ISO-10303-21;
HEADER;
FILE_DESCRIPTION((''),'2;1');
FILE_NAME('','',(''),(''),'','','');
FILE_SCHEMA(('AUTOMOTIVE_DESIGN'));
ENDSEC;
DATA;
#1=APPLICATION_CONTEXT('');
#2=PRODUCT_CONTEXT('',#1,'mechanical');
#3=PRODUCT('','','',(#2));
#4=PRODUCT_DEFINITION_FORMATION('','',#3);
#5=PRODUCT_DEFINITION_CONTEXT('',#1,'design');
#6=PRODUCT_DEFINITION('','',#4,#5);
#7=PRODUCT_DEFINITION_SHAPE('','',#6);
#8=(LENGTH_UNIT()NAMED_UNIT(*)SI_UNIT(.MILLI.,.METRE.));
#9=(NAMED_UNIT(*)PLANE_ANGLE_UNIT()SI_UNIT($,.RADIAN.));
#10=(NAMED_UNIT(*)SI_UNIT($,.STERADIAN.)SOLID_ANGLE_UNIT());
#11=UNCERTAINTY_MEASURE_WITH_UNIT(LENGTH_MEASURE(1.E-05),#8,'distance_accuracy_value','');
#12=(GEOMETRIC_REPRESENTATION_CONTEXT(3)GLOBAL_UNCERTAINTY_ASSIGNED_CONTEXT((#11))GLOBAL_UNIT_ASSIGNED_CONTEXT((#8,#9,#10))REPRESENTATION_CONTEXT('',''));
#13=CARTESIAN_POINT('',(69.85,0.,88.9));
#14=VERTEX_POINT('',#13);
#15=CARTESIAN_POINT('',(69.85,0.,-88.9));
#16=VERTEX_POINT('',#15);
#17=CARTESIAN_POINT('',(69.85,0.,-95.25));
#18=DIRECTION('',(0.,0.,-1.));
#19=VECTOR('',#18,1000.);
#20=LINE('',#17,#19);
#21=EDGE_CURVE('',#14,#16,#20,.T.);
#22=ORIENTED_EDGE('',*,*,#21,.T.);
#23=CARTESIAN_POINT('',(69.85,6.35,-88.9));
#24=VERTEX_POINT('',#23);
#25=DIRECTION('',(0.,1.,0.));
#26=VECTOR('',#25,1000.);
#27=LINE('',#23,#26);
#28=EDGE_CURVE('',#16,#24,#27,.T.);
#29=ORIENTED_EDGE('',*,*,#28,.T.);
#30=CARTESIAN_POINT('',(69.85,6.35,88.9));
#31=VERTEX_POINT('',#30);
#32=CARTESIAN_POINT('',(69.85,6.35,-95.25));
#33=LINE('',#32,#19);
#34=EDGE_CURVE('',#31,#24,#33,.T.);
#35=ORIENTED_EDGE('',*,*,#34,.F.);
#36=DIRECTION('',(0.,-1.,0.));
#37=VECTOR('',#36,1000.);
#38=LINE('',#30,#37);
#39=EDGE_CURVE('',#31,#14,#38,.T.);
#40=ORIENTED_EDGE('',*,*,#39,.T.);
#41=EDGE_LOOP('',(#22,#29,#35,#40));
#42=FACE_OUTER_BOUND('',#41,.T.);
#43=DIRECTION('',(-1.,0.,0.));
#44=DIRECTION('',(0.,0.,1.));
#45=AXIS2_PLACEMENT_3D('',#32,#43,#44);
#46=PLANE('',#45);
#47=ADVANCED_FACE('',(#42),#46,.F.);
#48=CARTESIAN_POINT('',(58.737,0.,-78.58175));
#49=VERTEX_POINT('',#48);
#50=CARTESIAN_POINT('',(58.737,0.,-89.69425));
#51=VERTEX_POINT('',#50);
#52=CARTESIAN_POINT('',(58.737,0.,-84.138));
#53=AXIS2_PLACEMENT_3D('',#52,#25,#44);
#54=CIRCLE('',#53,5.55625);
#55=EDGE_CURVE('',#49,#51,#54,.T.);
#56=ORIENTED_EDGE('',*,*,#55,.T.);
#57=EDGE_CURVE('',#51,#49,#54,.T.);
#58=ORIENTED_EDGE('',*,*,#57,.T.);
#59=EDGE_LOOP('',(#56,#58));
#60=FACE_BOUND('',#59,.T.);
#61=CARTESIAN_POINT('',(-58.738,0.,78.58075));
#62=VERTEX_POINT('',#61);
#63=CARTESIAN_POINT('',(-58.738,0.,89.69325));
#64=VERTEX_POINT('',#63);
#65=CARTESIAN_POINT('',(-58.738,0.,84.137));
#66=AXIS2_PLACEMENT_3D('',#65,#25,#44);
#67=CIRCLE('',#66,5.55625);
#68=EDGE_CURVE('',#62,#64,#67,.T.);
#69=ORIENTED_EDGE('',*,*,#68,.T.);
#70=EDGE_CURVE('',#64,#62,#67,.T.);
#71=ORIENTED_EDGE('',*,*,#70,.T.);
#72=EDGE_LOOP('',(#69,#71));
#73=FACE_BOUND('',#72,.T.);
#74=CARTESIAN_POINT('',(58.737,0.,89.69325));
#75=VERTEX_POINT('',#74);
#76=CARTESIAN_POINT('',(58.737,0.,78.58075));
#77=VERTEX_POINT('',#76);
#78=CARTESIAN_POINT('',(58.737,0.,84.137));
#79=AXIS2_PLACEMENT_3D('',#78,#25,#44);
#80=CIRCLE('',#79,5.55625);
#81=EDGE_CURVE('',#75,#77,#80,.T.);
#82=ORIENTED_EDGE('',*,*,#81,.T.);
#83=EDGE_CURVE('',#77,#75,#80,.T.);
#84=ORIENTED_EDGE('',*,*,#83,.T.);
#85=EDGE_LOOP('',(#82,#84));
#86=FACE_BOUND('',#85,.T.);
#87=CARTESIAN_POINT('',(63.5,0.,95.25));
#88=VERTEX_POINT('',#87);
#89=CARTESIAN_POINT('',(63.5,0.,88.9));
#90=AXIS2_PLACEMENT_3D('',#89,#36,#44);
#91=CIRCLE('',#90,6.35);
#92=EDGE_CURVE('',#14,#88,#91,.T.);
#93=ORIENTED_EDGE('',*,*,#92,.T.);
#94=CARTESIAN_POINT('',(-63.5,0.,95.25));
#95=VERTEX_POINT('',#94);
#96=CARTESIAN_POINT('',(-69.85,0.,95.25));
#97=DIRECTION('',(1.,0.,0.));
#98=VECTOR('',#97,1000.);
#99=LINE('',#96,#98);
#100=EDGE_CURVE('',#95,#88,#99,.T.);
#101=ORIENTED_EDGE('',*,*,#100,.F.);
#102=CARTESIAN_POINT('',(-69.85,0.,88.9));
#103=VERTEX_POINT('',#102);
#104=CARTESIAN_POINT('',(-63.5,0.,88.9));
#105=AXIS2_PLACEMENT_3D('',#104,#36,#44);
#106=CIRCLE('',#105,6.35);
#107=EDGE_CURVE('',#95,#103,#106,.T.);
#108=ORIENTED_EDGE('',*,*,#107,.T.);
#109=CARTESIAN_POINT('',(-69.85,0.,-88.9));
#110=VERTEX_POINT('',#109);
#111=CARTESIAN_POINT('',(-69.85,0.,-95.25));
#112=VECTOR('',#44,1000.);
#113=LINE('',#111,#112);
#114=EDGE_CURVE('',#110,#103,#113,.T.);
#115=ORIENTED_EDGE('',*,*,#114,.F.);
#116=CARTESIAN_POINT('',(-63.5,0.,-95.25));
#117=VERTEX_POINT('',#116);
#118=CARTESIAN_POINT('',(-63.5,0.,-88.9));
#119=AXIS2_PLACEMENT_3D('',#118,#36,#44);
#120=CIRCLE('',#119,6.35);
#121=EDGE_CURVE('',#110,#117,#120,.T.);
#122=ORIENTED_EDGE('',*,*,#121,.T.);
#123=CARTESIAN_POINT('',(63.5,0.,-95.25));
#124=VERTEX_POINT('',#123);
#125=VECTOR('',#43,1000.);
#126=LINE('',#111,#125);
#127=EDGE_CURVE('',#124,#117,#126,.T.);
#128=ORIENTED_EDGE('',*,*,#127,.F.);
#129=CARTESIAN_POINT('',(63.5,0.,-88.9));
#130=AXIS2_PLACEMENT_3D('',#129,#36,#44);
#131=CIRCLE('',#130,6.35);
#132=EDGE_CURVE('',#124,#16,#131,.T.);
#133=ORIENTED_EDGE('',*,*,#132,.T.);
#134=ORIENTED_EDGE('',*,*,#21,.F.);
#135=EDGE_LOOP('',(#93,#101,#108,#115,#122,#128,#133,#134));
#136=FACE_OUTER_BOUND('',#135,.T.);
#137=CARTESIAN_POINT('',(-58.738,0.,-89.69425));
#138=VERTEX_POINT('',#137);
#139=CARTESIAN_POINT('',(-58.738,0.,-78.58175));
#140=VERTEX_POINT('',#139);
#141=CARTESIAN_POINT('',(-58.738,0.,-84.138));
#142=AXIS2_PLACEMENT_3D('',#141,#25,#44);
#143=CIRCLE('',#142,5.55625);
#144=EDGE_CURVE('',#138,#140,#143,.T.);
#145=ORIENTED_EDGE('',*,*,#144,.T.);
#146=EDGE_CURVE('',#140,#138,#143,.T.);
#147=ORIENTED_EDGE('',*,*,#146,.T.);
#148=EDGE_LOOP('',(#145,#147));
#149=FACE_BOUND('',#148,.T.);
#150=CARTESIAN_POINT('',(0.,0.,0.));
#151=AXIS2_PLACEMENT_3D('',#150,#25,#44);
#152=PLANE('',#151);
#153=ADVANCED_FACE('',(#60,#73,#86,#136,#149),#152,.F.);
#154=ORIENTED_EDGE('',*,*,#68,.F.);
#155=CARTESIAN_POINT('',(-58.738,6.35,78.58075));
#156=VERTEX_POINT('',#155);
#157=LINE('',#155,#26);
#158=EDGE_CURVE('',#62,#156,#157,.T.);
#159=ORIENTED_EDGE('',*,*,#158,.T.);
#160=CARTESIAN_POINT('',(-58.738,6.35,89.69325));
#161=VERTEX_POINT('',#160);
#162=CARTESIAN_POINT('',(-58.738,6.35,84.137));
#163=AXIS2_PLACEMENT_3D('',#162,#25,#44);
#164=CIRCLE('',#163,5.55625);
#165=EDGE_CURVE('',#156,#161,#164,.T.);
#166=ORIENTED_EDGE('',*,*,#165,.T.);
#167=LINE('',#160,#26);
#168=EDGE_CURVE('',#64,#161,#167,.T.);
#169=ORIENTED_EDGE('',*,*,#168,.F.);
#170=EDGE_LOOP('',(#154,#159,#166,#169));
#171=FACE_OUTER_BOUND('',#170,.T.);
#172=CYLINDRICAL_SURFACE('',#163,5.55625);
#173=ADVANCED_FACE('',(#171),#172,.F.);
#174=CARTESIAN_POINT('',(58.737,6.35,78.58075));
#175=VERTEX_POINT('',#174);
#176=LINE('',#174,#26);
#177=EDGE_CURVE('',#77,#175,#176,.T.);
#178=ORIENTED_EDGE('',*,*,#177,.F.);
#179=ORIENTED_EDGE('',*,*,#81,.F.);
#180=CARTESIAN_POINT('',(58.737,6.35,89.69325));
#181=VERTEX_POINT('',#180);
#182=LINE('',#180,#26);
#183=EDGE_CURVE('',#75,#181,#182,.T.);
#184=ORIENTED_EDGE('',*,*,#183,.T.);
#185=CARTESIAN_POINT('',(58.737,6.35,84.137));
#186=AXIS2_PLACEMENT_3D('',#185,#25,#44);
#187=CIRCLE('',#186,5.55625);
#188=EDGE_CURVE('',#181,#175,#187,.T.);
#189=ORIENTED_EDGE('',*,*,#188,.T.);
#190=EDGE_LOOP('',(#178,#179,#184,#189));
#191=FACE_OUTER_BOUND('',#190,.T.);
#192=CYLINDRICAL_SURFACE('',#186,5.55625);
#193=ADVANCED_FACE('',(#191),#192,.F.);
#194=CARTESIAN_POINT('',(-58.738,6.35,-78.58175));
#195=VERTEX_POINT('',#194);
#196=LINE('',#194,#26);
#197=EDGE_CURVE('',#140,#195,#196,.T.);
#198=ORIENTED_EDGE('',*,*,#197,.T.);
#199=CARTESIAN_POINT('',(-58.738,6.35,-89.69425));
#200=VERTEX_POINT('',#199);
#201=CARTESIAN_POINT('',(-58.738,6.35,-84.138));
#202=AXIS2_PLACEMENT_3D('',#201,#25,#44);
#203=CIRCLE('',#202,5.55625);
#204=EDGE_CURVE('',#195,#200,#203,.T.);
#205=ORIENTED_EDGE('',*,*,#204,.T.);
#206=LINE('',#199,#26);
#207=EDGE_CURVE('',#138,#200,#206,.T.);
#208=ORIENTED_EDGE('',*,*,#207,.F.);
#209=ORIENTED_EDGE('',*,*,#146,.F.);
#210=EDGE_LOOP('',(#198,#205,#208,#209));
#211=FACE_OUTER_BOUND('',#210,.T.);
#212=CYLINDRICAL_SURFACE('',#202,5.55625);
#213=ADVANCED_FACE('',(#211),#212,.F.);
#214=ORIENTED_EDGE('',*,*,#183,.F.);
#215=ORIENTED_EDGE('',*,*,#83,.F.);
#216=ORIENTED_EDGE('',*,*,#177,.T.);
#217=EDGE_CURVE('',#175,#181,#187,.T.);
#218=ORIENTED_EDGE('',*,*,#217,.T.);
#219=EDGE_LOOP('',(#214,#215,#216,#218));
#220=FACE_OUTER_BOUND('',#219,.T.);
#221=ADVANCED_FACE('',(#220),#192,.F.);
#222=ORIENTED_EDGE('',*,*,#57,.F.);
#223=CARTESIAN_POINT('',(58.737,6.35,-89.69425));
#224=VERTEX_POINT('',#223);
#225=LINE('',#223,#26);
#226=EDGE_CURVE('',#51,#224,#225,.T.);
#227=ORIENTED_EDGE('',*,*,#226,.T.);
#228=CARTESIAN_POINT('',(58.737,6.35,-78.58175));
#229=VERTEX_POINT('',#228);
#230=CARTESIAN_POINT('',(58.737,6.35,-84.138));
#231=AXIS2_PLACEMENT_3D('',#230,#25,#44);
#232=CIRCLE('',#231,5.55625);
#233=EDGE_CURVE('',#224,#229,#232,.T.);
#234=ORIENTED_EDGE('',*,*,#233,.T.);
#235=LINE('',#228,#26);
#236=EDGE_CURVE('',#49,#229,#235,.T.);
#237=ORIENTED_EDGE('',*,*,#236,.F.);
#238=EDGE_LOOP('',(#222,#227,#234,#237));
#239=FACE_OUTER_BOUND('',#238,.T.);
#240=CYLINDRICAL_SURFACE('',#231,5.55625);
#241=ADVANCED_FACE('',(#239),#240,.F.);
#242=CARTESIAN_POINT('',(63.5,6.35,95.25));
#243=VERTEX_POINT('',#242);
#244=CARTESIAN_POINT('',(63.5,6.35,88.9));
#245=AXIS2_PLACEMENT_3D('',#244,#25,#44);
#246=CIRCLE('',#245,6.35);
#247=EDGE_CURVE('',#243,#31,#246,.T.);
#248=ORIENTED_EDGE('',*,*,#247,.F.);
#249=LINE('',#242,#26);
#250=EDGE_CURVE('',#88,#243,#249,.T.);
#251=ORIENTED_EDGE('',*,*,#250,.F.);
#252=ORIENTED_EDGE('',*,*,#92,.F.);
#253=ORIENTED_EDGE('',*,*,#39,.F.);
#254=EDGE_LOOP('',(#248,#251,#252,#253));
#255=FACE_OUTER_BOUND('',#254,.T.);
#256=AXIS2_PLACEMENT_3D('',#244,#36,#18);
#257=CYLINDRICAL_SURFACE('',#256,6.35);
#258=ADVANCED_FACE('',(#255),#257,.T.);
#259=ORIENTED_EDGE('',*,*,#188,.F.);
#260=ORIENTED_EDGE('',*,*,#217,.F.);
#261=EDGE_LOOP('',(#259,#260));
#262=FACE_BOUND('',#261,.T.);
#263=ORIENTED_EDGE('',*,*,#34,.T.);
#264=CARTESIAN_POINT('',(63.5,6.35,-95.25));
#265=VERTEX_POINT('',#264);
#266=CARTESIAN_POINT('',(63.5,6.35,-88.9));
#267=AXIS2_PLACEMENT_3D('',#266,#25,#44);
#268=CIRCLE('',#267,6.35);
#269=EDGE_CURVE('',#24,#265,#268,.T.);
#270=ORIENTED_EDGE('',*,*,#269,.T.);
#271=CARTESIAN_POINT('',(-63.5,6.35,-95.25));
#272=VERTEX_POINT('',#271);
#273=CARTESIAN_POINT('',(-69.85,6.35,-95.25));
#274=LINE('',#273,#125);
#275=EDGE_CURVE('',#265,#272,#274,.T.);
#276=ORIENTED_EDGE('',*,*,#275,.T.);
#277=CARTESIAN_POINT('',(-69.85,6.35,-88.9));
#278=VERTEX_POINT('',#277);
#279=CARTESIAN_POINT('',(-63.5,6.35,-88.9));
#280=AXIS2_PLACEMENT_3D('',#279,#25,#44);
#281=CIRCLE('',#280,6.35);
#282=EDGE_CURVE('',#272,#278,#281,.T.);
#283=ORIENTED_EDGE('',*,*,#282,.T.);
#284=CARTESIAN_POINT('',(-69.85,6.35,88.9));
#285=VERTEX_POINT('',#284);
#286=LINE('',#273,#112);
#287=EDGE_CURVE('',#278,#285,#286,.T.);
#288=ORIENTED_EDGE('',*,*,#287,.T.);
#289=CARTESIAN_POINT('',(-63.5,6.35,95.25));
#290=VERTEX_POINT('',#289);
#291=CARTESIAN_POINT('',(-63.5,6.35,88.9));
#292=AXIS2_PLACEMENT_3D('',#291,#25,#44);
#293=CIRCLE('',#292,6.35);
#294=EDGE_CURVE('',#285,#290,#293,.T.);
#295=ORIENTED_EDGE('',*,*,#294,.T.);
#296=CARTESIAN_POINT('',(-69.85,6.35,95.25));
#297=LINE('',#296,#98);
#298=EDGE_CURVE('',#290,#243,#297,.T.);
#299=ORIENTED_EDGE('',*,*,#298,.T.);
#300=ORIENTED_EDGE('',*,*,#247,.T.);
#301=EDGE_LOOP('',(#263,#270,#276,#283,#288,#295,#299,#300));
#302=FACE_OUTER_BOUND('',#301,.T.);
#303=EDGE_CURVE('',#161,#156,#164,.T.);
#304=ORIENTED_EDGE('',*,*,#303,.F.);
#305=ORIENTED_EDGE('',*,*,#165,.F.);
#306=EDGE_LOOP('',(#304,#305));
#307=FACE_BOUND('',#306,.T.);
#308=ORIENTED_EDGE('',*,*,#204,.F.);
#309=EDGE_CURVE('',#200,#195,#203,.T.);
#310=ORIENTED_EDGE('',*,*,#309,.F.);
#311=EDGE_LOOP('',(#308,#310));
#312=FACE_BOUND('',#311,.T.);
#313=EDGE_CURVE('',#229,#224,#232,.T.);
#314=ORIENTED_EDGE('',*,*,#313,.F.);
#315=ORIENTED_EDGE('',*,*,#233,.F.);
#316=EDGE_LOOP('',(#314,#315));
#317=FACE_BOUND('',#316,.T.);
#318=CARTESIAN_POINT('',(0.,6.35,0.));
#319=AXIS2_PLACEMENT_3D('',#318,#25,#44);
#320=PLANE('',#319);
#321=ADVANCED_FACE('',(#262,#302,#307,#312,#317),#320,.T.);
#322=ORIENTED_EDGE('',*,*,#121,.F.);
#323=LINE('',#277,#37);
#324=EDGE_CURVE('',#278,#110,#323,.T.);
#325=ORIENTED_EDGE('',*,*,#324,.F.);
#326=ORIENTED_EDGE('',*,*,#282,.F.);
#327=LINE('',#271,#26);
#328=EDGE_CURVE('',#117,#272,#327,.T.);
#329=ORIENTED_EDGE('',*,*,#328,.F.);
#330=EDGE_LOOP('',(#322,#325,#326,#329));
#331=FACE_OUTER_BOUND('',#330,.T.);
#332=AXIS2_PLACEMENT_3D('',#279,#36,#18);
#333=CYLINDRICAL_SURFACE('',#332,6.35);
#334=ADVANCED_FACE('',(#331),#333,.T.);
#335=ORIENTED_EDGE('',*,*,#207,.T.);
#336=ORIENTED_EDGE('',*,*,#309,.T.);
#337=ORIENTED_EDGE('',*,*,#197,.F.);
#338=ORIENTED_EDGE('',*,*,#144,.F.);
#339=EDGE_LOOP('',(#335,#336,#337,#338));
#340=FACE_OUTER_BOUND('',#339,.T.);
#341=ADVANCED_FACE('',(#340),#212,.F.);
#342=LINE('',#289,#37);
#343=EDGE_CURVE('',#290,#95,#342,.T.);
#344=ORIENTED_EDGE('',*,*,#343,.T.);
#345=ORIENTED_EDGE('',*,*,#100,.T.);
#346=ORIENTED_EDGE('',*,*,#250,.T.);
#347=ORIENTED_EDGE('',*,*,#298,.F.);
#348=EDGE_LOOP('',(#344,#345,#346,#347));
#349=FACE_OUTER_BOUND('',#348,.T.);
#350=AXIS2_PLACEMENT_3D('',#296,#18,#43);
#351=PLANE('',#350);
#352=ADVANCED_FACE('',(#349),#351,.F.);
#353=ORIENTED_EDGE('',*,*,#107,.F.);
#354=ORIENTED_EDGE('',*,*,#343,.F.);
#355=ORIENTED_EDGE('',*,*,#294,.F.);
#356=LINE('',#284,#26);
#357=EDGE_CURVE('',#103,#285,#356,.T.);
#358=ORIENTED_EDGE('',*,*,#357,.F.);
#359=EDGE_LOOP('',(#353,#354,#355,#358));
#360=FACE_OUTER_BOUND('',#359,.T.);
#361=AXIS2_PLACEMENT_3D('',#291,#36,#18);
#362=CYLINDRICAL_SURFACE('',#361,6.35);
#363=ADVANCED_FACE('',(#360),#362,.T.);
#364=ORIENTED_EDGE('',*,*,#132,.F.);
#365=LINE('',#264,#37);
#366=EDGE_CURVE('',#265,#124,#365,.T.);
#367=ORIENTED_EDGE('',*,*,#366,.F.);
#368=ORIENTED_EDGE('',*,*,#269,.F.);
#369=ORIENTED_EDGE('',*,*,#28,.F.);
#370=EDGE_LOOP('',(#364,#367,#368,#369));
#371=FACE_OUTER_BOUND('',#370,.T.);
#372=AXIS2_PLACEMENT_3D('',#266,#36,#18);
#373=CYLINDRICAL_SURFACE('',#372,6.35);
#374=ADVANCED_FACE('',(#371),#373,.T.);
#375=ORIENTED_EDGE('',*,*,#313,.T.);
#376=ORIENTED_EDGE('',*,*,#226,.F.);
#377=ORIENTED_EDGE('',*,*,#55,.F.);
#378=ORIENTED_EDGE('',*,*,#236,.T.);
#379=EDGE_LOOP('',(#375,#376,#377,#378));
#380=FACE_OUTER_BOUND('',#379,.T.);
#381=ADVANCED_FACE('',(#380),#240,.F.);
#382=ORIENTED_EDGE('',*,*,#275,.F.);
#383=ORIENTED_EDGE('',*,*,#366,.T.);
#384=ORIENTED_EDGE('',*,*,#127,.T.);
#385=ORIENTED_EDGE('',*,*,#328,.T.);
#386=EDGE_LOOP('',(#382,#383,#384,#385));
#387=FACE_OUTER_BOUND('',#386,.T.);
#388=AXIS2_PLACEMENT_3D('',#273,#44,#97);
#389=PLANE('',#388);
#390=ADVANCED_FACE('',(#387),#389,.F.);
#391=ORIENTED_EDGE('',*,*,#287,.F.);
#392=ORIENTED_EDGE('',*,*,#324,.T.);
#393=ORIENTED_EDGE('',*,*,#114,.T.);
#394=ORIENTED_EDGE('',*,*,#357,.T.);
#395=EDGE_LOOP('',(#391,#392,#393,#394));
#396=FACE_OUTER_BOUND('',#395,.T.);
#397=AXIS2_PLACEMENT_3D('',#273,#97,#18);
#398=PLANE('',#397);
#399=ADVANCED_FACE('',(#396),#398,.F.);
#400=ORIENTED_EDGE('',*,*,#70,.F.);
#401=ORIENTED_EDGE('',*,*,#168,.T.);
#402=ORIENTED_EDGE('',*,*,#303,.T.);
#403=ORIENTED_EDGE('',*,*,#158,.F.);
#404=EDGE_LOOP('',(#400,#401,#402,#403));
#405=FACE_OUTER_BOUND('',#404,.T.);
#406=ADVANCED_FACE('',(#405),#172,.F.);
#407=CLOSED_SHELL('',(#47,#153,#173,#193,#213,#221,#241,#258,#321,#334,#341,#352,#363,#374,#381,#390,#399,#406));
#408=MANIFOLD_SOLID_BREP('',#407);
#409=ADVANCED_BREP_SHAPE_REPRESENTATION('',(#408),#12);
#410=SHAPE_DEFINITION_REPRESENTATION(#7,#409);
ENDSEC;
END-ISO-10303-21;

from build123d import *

# Parameters (mm, degrees)
SKETCH1_W                      = 139.7
SKETCH1_H                      = 190.5
BOSS_EXTRUDE1_DEPTH            = 6.35
FILLET1_R                      = 6.35
F_7_16_0_4375_DIAMETER_HOLE1_D = 11.1125
LPATTERN1_COUNT                = 2
LPATTERN1_PITCH                = 168.275
LPATTERN1_COUNT_DIR2           = 2
LPATTERN1_PITCH_DIR2           = 117.475


with BuildPart() as part:
    # Sketch1 → Boss-Extrude1 (new body)
    with BuildSketch(Plane(origin=(0, 0, 0), x_dir=(1, 0, 0), z_dir=(0, 1, 0))):
        Rectangle(SKETCH1_W, SKETCH1_H)
    extrude(amount=BOSS_EXTRUDE1_DEPTH)

    # Fillet1
    fillet1_edges = [part.edges().sort_by_distance(p)[0] for p in [
        (-69.85, 3.175, -95.25),
        (69.85, 3.175, -95.25),
        (69.85, 3.175, 95.25),
        (-69.85, 3.175, 95.25),
    ]]
    fillet(fillet1_edges, radius=FILLET1_R)

    # 7/16 (0.4375) Diameter Hole1 (through all)
    with Locations(Plane(origin=(0, 6.35, 0), x_dir=(1, 0, 0), z_dir=(0, 1, 0))):
        with Locations((-58.738, 84.138)):
            f_7_16_0_4375_diameter_hole1 = Hole(F_7_16_0_4375_DIAMETER_HOLE1_D / 2)

    # LPattern1: 7_16 _0.4375_ Diameter Hole1 2 × 2
    with Locations(*[(j * LPATTERN1_PITCH_DIR2, 0, i * LPATTERN1_PITCH) for i in range(LPATTERN1_COUNT) for j in range(LPATTERN1_COUNT_DIR2) if (i, j) != (0, 0)]):
        add(f_7_16_0_4375_diameter_hole1, mode=Mode.SUBTRACT)


solid = part.part
